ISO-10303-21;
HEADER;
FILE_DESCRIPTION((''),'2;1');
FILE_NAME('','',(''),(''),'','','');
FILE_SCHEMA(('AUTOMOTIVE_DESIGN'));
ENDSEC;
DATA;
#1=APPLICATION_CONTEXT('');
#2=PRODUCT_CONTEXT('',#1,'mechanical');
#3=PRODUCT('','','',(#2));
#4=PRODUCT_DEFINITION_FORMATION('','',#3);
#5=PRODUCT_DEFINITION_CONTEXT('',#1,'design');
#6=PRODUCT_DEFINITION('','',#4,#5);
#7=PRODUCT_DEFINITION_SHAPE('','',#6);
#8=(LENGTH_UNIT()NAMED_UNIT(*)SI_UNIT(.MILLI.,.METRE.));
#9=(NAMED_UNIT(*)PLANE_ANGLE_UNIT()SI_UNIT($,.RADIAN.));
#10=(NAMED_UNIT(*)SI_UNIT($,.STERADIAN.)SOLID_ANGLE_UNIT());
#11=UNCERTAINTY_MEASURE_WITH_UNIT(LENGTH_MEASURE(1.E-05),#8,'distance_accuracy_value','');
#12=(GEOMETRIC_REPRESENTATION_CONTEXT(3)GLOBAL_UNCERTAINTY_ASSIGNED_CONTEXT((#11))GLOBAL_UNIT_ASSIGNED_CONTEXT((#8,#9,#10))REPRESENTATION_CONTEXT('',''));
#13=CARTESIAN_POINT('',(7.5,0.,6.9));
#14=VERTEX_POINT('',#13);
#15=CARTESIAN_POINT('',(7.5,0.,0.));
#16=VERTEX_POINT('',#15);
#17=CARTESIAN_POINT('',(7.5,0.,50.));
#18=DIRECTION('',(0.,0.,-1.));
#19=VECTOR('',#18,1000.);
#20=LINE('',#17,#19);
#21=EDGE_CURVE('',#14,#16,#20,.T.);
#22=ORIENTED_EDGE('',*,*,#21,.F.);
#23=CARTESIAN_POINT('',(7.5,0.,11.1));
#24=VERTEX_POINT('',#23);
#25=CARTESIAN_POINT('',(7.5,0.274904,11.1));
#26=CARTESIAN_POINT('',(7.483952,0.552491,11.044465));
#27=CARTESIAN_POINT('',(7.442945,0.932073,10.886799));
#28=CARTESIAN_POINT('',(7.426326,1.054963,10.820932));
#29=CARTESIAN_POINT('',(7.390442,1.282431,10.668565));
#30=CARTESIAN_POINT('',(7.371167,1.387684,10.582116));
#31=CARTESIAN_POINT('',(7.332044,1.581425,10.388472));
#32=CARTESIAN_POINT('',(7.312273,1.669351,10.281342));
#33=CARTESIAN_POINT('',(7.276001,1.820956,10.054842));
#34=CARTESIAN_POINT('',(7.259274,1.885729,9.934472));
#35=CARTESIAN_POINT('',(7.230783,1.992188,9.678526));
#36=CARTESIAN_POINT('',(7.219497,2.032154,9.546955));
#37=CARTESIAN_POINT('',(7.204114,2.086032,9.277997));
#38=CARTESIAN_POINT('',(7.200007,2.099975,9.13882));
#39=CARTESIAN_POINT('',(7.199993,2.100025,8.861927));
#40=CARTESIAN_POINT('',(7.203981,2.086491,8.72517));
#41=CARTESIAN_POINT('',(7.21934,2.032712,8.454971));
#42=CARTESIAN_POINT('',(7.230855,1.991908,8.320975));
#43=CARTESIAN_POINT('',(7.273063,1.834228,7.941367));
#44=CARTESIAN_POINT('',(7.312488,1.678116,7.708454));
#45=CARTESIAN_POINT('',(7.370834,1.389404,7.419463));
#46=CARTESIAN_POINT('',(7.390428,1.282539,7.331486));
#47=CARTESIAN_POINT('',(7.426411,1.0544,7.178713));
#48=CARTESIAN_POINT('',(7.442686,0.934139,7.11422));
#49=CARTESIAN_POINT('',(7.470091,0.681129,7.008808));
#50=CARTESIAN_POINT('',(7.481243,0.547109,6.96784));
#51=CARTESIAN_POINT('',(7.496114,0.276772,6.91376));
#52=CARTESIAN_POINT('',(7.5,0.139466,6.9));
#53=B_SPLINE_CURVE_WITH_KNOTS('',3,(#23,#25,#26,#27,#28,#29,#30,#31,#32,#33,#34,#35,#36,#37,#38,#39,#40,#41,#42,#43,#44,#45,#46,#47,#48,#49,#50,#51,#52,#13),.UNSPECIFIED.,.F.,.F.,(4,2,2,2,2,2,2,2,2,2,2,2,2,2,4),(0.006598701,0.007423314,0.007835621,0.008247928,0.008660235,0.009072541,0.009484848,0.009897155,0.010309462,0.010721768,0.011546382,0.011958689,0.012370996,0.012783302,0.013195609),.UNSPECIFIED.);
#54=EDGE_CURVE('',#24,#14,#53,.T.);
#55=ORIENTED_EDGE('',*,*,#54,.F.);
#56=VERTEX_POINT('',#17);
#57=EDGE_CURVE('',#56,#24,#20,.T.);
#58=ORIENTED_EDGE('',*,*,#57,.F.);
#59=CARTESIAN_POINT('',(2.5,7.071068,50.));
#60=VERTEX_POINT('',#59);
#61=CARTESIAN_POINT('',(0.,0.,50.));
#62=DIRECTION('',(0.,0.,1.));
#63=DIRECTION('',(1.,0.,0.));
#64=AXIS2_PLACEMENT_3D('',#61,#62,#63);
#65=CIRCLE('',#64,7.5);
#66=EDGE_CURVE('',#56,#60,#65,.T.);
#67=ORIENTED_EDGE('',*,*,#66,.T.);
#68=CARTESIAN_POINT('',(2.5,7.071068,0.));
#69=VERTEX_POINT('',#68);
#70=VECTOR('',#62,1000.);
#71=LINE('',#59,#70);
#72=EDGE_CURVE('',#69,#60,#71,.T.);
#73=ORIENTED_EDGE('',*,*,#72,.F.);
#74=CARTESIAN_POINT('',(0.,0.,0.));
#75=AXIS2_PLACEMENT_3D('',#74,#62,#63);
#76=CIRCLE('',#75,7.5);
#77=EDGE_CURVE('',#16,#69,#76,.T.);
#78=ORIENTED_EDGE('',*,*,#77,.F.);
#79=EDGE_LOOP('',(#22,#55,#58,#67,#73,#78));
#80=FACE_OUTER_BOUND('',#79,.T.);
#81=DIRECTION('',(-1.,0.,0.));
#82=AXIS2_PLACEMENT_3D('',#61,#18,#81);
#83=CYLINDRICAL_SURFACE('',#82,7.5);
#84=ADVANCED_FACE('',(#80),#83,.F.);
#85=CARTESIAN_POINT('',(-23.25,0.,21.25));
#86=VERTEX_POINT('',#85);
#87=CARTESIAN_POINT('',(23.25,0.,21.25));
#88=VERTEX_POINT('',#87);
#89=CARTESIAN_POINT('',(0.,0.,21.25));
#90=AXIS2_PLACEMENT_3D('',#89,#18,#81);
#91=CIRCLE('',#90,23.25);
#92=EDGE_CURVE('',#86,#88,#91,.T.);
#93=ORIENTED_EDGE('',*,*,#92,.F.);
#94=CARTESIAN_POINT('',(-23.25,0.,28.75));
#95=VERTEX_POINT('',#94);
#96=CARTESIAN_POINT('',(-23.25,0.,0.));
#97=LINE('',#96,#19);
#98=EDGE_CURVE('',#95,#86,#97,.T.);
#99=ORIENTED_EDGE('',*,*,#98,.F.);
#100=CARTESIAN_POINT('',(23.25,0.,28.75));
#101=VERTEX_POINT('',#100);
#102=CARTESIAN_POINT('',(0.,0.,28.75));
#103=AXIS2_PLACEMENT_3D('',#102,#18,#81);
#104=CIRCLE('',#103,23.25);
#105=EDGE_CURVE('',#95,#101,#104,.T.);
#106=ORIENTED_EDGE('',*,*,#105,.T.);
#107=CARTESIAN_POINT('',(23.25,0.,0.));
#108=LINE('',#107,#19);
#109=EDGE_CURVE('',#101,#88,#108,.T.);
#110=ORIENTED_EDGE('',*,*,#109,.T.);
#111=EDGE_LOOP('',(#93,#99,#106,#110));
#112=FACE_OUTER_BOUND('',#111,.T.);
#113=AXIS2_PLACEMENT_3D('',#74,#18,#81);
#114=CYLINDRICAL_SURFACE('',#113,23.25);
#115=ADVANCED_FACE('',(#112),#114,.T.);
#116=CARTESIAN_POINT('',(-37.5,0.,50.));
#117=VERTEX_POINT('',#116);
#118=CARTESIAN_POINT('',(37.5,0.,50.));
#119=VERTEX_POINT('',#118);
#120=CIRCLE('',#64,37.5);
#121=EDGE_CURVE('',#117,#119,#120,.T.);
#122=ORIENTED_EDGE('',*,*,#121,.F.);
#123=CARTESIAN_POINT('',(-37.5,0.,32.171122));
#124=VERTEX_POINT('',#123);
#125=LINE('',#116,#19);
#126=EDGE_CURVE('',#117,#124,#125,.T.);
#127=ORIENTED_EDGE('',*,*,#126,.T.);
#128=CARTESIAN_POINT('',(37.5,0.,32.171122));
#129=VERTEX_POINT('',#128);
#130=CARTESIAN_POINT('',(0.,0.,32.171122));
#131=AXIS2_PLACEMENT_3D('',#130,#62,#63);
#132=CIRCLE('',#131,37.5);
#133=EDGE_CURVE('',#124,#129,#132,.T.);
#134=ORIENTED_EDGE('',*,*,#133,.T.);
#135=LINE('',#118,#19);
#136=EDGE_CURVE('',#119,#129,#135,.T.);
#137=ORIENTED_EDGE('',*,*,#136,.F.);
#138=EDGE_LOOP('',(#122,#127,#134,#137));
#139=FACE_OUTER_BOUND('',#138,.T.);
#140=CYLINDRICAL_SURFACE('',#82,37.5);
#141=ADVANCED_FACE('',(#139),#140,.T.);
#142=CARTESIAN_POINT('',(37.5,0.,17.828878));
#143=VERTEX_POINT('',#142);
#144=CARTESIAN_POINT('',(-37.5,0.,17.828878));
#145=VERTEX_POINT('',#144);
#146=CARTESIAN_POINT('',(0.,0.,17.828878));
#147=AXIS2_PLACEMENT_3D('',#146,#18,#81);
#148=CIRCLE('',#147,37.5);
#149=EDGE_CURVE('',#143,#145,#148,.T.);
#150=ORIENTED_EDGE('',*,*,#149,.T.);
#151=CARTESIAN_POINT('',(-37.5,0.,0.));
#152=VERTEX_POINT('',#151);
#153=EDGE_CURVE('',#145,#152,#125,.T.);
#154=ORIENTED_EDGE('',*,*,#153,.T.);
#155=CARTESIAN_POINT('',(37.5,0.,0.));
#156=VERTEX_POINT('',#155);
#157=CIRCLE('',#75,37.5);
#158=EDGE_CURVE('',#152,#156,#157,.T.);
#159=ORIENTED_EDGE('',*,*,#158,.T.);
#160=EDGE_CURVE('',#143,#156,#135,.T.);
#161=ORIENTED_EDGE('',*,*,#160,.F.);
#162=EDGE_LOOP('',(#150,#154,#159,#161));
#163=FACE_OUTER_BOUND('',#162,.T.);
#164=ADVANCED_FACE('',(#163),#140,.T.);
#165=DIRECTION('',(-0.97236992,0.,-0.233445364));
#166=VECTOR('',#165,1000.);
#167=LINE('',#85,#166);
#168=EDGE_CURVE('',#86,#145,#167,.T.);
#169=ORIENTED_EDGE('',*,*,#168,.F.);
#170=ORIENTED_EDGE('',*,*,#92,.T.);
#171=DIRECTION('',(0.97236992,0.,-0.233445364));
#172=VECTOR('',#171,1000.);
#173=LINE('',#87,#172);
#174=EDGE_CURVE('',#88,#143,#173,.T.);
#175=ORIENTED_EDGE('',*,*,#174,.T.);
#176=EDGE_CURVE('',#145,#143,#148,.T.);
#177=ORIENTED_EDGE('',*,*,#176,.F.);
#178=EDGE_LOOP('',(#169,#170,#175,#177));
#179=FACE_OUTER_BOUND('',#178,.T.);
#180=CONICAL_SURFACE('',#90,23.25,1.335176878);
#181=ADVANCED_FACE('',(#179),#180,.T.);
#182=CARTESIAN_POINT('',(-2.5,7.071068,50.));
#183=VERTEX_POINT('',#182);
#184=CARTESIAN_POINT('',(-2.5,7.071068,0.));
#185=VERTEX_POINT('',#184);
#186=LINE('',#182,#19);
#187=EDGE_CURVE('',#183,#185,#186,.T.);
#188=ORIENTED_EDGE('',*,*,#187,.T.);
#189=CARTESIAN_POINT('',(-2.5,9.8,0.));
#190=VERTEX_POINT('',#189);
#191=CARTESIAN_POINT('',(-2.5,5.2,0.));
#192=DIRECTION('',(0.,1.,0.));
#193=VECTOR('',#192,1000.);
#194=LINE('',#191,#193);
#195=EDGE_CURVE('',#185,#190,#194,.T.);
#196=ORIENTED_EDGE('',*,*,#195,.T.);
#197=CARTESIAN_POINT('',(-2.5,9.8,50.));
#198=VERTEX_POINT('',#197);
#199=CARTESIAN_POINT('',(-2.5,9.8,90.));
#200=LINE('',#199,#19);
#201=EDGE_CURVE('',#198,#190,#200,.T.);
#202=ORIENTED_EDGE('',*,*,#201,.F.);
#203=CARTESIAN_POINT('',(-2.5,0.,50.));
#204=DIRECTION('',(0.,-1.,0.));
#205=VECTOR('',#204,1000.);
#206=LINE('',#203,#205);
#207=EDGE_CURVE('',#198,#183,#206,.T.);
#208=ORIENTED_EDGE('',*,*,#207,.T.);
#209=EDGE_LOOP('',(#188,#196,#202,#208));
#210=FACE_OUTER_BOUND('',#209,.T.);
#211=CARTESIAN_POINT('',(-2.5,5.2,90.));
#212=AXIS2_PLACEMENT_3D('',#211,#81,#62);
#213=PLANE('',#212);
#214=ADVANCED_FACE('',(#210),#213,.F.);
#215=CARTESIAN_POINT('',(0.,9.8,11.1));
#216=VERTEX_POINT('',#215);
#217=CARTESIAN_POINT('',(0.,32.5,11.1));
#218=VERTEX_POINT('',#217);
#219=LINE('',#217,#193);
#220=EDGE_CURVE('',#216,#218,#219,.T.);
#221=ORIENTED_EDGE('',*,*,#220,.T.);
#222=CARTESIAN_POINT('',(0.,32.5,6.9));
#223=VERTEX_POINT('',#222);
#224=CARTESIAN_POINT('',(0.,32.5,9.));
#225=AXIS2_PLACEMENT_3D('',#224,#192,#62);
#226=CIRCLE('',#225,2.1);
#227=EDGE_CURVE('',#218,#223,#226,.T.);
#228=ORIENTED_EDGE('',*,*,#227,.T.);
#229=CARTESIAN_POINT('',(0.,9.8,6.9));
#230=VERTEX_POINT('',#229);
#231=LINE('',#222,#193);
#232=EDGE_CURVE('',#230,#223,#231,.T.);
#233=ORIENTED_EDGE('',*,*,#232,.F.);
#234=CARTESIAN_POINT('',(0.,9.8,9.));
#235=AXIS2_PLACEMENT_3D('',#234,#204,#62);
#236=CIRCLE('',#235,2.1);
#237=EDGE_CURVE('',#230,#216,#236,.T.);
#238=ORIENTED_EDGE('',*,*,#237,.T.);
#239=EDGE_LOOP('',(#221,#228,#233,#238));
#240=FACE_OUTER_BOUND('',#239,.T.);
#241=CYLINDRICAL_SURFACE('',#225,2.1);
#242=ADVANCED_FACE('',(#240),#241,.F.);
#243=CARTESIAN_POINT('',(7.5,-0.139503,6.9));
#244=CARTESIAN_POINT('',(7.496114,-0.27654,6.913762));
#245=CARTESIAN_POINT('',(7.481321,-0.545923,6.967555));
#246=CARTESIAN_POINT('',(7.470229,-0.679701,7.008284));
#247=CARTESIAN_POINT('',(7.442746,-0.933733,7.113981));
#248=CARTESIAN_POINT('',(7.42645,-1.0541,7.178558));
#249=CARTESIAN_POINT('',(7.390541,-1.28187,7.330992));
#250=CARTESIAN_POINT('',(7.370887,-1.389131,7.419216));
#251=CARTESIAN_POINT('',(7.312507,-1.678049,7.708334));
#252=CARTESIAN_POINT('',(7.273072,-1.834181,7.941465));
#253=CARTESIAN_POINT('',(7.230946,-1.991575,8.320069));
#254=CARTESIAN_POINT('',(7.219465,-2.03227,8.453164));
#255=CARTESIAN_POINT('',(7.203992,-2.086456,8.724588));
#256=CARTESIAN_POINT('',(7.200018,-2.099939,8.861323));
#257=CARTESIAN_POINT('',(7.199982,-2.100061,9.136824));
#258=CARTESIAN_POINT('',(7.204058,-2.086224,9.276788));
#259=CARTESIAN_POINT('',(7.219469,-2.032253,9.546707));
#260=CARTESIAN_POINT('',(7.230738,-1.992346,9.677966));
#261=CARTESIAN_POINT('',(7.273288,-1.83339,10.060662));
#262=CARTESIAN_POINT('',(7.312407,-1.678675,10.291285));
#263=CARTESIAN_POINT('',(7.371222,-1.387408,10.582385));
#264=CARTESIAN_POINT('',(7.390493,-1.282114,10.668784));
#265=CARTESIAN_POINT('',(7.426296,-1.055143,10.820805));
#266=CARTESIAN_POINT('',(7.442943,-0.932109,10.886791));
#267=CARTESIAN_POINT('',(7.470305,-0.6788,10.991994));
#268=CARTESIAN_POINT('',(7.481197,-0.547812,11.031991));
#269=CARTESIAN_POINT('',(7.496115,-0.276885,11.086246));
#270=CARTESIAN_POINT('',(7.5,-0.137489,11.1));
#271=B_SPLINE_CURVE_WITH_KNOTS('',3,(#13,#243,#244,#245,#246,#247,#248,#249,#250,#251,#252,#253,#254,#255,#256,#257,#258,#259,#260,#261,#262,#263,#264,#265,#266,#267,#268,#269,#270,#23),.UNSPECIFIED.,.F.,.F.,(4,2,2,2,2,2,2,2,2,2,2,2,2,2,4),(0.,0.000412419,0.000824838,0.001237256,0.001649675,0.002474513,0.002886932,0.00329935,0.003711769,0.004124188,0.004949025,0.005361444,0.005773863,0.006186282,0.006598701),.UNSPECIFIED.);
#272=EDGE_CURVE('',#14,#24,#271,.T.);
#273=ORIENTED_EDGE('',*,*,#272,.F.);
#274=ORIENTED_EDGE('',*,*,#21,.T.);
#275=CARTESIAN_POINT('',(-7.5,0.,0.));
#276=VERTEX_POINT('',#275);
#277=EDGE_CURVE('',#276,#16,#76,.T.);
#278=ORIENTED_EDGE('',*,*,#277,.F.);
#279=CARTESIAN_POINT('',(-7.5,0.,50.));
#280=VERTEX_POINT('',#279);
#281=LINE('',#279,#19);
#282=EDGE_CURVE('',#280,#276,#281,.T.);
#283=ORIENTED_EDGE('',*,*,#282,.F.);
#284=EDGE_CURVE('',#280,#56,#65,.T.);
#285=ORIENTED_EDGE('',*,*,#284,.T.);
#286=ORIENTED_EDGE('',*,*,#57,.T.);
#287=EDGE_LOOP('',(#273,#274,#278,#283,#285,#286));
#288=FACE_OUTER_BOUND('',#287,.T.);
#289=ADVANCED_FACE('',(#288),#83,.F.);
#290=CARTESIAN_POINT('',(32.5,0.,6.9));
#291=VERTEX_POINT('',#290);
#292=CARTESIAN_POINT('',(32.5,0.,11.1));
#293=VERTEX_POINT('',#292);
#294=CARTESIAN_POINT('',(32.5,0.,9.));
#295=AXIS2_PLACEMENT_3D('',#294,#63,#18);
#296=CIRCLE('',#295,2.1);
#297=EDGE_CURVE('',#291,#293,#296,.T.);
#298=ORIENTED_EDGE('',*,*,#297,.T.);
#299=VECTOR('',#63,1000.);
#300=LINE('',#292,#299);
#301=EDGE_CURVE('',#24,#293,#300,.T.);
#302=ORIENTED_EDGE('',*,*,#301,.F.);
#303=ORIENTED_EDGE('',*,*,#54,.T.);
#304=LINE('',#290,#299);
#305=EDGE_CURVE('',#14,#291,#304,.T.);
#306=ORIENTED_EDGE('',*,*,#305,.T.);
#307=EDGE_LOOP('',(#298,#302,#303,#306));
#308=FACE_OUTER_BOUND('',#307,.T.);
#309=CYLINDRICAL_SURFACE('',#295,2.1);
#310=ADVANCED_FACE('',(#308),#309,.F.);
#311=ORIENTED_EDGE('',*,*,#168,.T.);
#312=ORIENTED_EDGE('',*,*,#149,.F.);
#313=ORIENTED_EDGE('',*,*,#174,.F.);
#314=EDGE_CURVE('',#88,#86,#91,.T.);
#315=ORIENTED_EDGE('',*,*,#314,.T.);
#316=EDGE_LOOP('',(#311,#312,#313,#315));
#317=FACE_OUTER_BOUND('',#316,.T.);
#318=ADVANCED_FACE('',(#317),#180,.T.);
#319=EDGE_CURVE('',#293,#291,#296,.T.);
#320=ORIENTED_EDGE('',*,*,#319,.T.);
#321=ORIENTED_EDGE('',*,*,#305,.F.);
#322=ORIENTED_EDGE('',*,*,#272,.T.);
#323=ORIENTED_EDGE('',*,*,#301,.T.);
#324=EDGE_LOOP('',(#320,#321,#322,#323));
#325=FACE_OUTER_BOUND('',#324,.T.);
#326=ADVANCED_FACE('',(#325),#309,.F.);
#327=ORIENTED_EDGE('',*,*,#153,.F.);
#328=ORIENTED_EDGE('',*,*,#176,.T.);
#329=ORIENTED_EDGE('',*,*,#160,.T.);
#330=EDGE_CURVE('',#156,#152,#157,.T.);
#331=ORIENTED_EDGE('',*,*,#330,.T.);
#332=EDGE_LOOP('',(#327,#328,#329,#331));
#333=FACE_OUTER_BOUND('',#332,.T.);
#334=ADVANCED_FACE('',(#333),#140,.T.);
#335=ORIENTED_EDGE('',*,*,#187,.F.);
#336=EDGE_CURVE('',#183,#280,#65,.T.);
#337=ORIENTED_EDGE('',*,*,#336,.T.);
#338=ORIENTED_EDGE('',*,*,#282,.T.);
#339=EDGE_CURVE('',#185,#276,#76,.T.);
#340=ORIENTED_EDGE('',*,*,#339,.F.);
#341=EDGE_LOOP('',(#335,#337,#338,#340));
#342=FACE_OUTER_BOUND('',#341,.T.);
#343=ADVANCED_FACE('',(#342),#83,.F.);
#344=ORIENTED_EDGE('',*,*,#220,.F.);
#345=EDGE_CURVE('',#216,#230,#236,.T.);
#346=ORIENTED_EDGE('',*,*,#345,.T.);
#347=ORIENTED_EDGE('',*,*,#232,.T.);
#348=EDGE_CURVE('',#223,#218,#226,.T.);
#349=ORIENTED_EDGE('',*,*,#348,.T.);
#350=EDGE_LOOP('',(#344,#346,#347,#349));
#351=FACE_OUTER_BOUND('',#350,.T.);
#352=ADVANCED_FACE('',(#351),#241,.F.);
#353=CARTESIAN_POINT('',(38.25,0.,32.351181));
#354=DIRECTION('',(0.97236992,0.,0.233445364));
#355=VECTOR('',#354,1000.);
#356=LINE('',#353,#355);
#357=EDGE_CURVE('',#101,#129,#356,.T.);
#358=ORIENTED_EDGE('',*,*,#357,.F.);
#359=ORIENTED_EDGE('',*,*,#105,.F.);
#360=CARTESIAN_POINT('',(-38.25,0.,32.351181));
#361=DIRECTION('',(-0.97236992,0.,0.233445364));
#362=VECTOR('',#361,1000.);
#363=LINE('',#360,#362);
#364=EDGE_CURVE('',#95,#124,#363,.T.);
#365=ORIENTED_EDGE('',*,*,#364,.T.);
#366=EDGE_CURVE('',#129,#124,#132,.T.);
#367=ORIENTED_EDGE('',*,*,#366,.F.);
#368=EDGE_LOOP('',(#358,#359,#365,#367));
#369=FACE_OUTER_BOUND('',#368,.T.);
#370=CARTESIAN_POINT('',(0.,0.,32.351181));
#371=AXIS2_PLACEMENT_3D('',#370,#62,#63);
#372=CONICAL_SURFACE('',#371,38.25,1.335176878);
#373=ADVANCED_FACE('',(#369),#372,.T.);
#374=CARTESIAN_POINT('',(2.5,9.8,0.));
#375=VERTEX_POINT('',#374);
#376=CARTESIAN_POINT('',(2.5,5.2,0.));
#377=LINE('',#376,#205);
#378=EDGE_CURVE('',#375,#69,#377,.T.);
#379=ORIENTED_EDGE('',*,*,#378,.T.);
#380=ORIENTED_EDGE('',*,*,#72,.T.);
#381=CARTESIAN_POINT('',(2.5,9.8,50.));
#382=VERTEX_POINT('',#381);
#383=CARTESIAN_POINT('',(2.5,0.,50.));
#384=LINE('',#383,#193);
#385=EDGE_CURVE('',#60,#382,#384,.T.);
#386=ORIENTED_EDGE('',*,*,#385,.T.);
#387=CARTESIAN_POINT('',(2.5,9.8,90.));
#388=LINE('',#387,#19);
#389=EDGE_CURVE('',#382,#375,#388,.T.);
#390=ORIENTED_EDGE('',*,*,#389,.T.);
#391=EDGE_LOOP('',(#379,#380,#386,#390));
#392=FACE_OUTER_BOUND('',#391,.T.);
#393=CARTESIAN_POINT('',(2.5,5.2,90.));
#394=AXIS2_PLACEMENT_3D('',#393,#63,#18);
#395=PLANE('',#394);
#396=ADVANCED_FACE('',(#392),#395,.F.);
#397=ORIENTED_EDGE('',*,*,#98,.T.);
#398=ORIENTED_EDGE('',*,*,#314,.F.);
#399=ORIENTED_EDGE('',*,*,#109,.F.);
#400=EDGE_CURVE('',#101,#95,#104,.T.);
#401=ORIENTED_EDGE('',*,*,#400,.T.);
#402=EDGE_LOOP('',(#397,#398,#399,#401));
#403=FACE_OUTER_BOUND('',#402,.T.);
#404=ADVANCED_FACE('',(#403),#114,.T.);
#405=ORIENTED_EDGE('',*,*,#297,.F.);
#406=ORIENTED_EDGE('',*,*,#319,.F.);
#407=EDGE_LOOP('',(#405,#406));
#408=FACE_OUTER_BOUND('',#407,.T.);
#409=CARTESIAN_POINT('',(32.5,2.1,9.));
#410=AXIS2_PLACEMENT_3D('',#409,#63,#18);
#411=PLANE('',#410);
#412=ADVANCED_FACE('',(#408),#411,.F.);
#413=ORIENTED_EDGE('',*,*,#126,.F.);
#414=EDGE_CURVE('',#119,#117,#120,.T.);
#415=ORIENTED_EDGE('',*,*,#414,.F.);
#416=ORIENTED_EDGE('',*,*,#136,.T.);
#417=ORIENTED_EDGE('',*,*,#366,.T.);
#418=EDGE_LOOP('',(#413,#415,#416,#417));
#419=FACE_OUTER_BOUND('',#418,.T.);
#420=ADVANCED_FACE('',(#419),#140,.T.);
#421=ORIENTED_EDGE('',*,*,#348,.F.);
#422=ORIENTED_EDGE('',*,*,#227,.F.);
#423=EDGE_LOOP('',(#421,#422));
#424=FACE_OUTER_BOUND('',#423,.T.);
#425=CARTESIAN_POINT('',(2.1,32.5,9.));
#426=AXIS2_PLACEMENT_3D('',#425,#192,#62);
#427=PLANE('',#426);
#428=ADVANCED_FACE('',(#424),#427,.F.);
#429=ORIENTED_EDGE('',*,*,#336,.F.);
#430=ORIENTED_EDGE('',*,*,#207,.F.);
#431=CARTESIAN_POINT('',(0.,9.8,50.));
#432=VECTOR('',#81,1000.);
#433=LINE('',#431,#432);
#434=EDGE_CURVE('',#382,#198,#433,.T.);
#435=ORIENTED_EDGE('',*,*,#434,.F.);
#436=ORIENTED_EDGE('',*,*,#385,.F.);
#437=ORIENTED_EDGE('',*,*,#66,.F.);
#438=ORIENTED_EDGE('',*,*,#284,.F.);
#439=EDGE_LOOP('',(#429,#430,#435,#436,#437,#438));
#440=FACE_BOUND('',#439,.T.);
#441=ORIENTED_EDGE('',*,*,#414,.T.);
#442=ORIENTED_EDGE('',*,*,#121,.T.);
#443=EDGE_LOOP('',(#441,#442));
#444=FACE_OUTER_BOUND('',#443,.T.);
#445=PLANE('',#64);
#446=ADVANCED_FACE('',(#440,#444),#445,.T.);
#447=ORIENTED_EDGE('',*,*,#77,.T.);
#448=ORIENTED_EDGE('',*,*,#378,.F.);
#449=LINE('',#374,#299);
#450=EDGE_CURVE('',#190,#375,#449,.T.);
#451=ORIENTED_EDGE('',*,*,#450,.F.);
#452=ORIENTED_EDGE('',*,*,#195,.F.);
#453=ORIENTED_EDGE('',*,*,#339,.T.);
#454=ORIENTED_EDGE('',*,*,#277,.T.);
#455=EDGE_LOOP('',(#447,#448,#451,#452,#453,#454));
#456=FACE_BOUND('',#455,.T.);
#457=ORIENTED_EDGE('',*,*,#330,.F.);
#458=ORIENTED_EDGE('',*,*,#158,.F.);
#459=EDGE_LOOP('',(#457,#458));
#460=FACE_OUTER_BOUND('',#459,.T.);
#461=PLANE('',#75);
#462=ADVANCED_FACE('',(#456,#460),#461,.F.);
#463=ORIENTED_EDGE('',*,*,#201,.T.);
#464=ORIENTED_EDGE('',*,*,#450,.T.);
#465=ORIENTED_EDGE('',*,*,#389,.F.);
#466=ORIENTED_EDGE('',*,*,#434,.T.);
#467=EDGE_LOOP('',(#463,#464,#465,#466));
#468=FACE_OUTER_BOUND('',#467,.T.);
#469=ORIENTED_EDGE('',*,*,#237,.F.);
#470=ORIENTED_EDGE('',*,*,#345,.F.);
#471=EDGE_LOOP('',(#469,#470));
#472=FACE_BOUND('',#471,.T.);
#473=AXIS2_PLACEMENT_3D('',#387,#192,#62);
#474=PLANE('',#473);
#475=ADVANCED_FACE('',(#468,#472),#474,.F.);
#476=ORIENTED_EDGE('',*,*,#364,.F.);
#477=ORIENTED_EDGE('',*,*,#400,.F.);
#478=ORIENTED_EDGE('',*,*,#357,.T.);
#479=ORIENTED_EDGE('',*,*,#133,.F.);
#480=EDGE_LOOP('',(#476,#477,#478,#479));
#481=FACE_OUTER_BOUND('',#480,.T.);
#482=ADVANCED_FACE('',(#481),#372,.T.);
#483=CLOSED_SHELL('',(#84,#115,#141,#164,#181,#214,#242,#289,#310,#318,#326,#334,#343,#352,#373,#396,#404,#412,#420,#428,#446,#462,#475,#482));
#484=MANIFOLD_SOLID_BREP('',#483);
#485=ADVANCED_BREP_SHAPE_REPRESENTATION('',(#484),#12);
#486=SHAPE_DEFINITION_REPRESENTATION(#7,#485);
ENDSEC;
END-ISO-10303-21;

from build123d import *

# Parameters (mm, degrees)
SKETCH_1_R          = 37.5
SKETCH_1_R_2        = 7.5
EXTRUDE_1_DEPTH     = 50
SKETCH_7_W          = 5
SKETCH_7_H          = 4.6
CUT_EXTRUDE_1_DEPTH = 90


with BuildPart() as part:
    # 草图1 → 凸台-拉伸1 (new body)
    with BuildSketch(Plane.XY):
        Circle(SKETCH_1_R)
        Circle(SKETCH_1_R_2, mode=Mode.SUBTRACT)
    extrude(amount=EXTRUDE_1_DEPTH)

    # 草图2 → 切除-旋转1 (revolve, cut)
    with BuildSketch(Plane(origin=(0, 0, 0), x_dir=(1, 0, 0), z_dir=(0, 1, 0))):
        Polygon((-38.25, -17.648818614), (-23.25, -21.25), (-23.25, -28.75), (-38.25, -32.351181386), align=None)
    revolve(axis=Axis((0, 0, 0), (0, 0, 1)), mode=Mode.SUBTRACT)

    # 草图3 → M5 螺纹孔2 (revolve, cut)
    with BuildSketch(Plane(origin=(0, 32.5, 9), x_dir=(0, 0, 1), z_dir=(1, 0, 0))):
        Polygon((0, 0), (0, 31.2618073), (2.1, 30), (2.1, 0), align=None)
    revolve(axis=Axis((0, 38.85, 9), (0, -1, 0)), mode=Mode.SUBTRACT)

    # 草图5 → M5 螺纹孔1 (revolve, cut)
    with BuildSketch(Plane(origin=(32.5, 0, 9), x_dir=(0, 0, -1), z_dir=(0, 1, 0))):
        Polygon((0, 0), (0, 31.2618073), (2.1, 30), (2.1, 0), align=None)
    revolve(axis=Axis((38.85, 0, 9), (-1, 0, 0)), mode=Mode.SUBTRACT)

    # 草图7 → 切除-拉伸1 (cut)
    with BuildSketch(Plane(origin=(0, 0, 0), x_dir=(-1, 0, 0), z_dir=(0, 0, -1))):
        with Locations((0, 7.5)):
            Rectangle(SKETCH_7_W, SKETCH_7_H)
    extrude(amount=-CUT_EXTRUDE_1_DEPTH, mode=Mode.SUBTRACT)


solid = part.part
